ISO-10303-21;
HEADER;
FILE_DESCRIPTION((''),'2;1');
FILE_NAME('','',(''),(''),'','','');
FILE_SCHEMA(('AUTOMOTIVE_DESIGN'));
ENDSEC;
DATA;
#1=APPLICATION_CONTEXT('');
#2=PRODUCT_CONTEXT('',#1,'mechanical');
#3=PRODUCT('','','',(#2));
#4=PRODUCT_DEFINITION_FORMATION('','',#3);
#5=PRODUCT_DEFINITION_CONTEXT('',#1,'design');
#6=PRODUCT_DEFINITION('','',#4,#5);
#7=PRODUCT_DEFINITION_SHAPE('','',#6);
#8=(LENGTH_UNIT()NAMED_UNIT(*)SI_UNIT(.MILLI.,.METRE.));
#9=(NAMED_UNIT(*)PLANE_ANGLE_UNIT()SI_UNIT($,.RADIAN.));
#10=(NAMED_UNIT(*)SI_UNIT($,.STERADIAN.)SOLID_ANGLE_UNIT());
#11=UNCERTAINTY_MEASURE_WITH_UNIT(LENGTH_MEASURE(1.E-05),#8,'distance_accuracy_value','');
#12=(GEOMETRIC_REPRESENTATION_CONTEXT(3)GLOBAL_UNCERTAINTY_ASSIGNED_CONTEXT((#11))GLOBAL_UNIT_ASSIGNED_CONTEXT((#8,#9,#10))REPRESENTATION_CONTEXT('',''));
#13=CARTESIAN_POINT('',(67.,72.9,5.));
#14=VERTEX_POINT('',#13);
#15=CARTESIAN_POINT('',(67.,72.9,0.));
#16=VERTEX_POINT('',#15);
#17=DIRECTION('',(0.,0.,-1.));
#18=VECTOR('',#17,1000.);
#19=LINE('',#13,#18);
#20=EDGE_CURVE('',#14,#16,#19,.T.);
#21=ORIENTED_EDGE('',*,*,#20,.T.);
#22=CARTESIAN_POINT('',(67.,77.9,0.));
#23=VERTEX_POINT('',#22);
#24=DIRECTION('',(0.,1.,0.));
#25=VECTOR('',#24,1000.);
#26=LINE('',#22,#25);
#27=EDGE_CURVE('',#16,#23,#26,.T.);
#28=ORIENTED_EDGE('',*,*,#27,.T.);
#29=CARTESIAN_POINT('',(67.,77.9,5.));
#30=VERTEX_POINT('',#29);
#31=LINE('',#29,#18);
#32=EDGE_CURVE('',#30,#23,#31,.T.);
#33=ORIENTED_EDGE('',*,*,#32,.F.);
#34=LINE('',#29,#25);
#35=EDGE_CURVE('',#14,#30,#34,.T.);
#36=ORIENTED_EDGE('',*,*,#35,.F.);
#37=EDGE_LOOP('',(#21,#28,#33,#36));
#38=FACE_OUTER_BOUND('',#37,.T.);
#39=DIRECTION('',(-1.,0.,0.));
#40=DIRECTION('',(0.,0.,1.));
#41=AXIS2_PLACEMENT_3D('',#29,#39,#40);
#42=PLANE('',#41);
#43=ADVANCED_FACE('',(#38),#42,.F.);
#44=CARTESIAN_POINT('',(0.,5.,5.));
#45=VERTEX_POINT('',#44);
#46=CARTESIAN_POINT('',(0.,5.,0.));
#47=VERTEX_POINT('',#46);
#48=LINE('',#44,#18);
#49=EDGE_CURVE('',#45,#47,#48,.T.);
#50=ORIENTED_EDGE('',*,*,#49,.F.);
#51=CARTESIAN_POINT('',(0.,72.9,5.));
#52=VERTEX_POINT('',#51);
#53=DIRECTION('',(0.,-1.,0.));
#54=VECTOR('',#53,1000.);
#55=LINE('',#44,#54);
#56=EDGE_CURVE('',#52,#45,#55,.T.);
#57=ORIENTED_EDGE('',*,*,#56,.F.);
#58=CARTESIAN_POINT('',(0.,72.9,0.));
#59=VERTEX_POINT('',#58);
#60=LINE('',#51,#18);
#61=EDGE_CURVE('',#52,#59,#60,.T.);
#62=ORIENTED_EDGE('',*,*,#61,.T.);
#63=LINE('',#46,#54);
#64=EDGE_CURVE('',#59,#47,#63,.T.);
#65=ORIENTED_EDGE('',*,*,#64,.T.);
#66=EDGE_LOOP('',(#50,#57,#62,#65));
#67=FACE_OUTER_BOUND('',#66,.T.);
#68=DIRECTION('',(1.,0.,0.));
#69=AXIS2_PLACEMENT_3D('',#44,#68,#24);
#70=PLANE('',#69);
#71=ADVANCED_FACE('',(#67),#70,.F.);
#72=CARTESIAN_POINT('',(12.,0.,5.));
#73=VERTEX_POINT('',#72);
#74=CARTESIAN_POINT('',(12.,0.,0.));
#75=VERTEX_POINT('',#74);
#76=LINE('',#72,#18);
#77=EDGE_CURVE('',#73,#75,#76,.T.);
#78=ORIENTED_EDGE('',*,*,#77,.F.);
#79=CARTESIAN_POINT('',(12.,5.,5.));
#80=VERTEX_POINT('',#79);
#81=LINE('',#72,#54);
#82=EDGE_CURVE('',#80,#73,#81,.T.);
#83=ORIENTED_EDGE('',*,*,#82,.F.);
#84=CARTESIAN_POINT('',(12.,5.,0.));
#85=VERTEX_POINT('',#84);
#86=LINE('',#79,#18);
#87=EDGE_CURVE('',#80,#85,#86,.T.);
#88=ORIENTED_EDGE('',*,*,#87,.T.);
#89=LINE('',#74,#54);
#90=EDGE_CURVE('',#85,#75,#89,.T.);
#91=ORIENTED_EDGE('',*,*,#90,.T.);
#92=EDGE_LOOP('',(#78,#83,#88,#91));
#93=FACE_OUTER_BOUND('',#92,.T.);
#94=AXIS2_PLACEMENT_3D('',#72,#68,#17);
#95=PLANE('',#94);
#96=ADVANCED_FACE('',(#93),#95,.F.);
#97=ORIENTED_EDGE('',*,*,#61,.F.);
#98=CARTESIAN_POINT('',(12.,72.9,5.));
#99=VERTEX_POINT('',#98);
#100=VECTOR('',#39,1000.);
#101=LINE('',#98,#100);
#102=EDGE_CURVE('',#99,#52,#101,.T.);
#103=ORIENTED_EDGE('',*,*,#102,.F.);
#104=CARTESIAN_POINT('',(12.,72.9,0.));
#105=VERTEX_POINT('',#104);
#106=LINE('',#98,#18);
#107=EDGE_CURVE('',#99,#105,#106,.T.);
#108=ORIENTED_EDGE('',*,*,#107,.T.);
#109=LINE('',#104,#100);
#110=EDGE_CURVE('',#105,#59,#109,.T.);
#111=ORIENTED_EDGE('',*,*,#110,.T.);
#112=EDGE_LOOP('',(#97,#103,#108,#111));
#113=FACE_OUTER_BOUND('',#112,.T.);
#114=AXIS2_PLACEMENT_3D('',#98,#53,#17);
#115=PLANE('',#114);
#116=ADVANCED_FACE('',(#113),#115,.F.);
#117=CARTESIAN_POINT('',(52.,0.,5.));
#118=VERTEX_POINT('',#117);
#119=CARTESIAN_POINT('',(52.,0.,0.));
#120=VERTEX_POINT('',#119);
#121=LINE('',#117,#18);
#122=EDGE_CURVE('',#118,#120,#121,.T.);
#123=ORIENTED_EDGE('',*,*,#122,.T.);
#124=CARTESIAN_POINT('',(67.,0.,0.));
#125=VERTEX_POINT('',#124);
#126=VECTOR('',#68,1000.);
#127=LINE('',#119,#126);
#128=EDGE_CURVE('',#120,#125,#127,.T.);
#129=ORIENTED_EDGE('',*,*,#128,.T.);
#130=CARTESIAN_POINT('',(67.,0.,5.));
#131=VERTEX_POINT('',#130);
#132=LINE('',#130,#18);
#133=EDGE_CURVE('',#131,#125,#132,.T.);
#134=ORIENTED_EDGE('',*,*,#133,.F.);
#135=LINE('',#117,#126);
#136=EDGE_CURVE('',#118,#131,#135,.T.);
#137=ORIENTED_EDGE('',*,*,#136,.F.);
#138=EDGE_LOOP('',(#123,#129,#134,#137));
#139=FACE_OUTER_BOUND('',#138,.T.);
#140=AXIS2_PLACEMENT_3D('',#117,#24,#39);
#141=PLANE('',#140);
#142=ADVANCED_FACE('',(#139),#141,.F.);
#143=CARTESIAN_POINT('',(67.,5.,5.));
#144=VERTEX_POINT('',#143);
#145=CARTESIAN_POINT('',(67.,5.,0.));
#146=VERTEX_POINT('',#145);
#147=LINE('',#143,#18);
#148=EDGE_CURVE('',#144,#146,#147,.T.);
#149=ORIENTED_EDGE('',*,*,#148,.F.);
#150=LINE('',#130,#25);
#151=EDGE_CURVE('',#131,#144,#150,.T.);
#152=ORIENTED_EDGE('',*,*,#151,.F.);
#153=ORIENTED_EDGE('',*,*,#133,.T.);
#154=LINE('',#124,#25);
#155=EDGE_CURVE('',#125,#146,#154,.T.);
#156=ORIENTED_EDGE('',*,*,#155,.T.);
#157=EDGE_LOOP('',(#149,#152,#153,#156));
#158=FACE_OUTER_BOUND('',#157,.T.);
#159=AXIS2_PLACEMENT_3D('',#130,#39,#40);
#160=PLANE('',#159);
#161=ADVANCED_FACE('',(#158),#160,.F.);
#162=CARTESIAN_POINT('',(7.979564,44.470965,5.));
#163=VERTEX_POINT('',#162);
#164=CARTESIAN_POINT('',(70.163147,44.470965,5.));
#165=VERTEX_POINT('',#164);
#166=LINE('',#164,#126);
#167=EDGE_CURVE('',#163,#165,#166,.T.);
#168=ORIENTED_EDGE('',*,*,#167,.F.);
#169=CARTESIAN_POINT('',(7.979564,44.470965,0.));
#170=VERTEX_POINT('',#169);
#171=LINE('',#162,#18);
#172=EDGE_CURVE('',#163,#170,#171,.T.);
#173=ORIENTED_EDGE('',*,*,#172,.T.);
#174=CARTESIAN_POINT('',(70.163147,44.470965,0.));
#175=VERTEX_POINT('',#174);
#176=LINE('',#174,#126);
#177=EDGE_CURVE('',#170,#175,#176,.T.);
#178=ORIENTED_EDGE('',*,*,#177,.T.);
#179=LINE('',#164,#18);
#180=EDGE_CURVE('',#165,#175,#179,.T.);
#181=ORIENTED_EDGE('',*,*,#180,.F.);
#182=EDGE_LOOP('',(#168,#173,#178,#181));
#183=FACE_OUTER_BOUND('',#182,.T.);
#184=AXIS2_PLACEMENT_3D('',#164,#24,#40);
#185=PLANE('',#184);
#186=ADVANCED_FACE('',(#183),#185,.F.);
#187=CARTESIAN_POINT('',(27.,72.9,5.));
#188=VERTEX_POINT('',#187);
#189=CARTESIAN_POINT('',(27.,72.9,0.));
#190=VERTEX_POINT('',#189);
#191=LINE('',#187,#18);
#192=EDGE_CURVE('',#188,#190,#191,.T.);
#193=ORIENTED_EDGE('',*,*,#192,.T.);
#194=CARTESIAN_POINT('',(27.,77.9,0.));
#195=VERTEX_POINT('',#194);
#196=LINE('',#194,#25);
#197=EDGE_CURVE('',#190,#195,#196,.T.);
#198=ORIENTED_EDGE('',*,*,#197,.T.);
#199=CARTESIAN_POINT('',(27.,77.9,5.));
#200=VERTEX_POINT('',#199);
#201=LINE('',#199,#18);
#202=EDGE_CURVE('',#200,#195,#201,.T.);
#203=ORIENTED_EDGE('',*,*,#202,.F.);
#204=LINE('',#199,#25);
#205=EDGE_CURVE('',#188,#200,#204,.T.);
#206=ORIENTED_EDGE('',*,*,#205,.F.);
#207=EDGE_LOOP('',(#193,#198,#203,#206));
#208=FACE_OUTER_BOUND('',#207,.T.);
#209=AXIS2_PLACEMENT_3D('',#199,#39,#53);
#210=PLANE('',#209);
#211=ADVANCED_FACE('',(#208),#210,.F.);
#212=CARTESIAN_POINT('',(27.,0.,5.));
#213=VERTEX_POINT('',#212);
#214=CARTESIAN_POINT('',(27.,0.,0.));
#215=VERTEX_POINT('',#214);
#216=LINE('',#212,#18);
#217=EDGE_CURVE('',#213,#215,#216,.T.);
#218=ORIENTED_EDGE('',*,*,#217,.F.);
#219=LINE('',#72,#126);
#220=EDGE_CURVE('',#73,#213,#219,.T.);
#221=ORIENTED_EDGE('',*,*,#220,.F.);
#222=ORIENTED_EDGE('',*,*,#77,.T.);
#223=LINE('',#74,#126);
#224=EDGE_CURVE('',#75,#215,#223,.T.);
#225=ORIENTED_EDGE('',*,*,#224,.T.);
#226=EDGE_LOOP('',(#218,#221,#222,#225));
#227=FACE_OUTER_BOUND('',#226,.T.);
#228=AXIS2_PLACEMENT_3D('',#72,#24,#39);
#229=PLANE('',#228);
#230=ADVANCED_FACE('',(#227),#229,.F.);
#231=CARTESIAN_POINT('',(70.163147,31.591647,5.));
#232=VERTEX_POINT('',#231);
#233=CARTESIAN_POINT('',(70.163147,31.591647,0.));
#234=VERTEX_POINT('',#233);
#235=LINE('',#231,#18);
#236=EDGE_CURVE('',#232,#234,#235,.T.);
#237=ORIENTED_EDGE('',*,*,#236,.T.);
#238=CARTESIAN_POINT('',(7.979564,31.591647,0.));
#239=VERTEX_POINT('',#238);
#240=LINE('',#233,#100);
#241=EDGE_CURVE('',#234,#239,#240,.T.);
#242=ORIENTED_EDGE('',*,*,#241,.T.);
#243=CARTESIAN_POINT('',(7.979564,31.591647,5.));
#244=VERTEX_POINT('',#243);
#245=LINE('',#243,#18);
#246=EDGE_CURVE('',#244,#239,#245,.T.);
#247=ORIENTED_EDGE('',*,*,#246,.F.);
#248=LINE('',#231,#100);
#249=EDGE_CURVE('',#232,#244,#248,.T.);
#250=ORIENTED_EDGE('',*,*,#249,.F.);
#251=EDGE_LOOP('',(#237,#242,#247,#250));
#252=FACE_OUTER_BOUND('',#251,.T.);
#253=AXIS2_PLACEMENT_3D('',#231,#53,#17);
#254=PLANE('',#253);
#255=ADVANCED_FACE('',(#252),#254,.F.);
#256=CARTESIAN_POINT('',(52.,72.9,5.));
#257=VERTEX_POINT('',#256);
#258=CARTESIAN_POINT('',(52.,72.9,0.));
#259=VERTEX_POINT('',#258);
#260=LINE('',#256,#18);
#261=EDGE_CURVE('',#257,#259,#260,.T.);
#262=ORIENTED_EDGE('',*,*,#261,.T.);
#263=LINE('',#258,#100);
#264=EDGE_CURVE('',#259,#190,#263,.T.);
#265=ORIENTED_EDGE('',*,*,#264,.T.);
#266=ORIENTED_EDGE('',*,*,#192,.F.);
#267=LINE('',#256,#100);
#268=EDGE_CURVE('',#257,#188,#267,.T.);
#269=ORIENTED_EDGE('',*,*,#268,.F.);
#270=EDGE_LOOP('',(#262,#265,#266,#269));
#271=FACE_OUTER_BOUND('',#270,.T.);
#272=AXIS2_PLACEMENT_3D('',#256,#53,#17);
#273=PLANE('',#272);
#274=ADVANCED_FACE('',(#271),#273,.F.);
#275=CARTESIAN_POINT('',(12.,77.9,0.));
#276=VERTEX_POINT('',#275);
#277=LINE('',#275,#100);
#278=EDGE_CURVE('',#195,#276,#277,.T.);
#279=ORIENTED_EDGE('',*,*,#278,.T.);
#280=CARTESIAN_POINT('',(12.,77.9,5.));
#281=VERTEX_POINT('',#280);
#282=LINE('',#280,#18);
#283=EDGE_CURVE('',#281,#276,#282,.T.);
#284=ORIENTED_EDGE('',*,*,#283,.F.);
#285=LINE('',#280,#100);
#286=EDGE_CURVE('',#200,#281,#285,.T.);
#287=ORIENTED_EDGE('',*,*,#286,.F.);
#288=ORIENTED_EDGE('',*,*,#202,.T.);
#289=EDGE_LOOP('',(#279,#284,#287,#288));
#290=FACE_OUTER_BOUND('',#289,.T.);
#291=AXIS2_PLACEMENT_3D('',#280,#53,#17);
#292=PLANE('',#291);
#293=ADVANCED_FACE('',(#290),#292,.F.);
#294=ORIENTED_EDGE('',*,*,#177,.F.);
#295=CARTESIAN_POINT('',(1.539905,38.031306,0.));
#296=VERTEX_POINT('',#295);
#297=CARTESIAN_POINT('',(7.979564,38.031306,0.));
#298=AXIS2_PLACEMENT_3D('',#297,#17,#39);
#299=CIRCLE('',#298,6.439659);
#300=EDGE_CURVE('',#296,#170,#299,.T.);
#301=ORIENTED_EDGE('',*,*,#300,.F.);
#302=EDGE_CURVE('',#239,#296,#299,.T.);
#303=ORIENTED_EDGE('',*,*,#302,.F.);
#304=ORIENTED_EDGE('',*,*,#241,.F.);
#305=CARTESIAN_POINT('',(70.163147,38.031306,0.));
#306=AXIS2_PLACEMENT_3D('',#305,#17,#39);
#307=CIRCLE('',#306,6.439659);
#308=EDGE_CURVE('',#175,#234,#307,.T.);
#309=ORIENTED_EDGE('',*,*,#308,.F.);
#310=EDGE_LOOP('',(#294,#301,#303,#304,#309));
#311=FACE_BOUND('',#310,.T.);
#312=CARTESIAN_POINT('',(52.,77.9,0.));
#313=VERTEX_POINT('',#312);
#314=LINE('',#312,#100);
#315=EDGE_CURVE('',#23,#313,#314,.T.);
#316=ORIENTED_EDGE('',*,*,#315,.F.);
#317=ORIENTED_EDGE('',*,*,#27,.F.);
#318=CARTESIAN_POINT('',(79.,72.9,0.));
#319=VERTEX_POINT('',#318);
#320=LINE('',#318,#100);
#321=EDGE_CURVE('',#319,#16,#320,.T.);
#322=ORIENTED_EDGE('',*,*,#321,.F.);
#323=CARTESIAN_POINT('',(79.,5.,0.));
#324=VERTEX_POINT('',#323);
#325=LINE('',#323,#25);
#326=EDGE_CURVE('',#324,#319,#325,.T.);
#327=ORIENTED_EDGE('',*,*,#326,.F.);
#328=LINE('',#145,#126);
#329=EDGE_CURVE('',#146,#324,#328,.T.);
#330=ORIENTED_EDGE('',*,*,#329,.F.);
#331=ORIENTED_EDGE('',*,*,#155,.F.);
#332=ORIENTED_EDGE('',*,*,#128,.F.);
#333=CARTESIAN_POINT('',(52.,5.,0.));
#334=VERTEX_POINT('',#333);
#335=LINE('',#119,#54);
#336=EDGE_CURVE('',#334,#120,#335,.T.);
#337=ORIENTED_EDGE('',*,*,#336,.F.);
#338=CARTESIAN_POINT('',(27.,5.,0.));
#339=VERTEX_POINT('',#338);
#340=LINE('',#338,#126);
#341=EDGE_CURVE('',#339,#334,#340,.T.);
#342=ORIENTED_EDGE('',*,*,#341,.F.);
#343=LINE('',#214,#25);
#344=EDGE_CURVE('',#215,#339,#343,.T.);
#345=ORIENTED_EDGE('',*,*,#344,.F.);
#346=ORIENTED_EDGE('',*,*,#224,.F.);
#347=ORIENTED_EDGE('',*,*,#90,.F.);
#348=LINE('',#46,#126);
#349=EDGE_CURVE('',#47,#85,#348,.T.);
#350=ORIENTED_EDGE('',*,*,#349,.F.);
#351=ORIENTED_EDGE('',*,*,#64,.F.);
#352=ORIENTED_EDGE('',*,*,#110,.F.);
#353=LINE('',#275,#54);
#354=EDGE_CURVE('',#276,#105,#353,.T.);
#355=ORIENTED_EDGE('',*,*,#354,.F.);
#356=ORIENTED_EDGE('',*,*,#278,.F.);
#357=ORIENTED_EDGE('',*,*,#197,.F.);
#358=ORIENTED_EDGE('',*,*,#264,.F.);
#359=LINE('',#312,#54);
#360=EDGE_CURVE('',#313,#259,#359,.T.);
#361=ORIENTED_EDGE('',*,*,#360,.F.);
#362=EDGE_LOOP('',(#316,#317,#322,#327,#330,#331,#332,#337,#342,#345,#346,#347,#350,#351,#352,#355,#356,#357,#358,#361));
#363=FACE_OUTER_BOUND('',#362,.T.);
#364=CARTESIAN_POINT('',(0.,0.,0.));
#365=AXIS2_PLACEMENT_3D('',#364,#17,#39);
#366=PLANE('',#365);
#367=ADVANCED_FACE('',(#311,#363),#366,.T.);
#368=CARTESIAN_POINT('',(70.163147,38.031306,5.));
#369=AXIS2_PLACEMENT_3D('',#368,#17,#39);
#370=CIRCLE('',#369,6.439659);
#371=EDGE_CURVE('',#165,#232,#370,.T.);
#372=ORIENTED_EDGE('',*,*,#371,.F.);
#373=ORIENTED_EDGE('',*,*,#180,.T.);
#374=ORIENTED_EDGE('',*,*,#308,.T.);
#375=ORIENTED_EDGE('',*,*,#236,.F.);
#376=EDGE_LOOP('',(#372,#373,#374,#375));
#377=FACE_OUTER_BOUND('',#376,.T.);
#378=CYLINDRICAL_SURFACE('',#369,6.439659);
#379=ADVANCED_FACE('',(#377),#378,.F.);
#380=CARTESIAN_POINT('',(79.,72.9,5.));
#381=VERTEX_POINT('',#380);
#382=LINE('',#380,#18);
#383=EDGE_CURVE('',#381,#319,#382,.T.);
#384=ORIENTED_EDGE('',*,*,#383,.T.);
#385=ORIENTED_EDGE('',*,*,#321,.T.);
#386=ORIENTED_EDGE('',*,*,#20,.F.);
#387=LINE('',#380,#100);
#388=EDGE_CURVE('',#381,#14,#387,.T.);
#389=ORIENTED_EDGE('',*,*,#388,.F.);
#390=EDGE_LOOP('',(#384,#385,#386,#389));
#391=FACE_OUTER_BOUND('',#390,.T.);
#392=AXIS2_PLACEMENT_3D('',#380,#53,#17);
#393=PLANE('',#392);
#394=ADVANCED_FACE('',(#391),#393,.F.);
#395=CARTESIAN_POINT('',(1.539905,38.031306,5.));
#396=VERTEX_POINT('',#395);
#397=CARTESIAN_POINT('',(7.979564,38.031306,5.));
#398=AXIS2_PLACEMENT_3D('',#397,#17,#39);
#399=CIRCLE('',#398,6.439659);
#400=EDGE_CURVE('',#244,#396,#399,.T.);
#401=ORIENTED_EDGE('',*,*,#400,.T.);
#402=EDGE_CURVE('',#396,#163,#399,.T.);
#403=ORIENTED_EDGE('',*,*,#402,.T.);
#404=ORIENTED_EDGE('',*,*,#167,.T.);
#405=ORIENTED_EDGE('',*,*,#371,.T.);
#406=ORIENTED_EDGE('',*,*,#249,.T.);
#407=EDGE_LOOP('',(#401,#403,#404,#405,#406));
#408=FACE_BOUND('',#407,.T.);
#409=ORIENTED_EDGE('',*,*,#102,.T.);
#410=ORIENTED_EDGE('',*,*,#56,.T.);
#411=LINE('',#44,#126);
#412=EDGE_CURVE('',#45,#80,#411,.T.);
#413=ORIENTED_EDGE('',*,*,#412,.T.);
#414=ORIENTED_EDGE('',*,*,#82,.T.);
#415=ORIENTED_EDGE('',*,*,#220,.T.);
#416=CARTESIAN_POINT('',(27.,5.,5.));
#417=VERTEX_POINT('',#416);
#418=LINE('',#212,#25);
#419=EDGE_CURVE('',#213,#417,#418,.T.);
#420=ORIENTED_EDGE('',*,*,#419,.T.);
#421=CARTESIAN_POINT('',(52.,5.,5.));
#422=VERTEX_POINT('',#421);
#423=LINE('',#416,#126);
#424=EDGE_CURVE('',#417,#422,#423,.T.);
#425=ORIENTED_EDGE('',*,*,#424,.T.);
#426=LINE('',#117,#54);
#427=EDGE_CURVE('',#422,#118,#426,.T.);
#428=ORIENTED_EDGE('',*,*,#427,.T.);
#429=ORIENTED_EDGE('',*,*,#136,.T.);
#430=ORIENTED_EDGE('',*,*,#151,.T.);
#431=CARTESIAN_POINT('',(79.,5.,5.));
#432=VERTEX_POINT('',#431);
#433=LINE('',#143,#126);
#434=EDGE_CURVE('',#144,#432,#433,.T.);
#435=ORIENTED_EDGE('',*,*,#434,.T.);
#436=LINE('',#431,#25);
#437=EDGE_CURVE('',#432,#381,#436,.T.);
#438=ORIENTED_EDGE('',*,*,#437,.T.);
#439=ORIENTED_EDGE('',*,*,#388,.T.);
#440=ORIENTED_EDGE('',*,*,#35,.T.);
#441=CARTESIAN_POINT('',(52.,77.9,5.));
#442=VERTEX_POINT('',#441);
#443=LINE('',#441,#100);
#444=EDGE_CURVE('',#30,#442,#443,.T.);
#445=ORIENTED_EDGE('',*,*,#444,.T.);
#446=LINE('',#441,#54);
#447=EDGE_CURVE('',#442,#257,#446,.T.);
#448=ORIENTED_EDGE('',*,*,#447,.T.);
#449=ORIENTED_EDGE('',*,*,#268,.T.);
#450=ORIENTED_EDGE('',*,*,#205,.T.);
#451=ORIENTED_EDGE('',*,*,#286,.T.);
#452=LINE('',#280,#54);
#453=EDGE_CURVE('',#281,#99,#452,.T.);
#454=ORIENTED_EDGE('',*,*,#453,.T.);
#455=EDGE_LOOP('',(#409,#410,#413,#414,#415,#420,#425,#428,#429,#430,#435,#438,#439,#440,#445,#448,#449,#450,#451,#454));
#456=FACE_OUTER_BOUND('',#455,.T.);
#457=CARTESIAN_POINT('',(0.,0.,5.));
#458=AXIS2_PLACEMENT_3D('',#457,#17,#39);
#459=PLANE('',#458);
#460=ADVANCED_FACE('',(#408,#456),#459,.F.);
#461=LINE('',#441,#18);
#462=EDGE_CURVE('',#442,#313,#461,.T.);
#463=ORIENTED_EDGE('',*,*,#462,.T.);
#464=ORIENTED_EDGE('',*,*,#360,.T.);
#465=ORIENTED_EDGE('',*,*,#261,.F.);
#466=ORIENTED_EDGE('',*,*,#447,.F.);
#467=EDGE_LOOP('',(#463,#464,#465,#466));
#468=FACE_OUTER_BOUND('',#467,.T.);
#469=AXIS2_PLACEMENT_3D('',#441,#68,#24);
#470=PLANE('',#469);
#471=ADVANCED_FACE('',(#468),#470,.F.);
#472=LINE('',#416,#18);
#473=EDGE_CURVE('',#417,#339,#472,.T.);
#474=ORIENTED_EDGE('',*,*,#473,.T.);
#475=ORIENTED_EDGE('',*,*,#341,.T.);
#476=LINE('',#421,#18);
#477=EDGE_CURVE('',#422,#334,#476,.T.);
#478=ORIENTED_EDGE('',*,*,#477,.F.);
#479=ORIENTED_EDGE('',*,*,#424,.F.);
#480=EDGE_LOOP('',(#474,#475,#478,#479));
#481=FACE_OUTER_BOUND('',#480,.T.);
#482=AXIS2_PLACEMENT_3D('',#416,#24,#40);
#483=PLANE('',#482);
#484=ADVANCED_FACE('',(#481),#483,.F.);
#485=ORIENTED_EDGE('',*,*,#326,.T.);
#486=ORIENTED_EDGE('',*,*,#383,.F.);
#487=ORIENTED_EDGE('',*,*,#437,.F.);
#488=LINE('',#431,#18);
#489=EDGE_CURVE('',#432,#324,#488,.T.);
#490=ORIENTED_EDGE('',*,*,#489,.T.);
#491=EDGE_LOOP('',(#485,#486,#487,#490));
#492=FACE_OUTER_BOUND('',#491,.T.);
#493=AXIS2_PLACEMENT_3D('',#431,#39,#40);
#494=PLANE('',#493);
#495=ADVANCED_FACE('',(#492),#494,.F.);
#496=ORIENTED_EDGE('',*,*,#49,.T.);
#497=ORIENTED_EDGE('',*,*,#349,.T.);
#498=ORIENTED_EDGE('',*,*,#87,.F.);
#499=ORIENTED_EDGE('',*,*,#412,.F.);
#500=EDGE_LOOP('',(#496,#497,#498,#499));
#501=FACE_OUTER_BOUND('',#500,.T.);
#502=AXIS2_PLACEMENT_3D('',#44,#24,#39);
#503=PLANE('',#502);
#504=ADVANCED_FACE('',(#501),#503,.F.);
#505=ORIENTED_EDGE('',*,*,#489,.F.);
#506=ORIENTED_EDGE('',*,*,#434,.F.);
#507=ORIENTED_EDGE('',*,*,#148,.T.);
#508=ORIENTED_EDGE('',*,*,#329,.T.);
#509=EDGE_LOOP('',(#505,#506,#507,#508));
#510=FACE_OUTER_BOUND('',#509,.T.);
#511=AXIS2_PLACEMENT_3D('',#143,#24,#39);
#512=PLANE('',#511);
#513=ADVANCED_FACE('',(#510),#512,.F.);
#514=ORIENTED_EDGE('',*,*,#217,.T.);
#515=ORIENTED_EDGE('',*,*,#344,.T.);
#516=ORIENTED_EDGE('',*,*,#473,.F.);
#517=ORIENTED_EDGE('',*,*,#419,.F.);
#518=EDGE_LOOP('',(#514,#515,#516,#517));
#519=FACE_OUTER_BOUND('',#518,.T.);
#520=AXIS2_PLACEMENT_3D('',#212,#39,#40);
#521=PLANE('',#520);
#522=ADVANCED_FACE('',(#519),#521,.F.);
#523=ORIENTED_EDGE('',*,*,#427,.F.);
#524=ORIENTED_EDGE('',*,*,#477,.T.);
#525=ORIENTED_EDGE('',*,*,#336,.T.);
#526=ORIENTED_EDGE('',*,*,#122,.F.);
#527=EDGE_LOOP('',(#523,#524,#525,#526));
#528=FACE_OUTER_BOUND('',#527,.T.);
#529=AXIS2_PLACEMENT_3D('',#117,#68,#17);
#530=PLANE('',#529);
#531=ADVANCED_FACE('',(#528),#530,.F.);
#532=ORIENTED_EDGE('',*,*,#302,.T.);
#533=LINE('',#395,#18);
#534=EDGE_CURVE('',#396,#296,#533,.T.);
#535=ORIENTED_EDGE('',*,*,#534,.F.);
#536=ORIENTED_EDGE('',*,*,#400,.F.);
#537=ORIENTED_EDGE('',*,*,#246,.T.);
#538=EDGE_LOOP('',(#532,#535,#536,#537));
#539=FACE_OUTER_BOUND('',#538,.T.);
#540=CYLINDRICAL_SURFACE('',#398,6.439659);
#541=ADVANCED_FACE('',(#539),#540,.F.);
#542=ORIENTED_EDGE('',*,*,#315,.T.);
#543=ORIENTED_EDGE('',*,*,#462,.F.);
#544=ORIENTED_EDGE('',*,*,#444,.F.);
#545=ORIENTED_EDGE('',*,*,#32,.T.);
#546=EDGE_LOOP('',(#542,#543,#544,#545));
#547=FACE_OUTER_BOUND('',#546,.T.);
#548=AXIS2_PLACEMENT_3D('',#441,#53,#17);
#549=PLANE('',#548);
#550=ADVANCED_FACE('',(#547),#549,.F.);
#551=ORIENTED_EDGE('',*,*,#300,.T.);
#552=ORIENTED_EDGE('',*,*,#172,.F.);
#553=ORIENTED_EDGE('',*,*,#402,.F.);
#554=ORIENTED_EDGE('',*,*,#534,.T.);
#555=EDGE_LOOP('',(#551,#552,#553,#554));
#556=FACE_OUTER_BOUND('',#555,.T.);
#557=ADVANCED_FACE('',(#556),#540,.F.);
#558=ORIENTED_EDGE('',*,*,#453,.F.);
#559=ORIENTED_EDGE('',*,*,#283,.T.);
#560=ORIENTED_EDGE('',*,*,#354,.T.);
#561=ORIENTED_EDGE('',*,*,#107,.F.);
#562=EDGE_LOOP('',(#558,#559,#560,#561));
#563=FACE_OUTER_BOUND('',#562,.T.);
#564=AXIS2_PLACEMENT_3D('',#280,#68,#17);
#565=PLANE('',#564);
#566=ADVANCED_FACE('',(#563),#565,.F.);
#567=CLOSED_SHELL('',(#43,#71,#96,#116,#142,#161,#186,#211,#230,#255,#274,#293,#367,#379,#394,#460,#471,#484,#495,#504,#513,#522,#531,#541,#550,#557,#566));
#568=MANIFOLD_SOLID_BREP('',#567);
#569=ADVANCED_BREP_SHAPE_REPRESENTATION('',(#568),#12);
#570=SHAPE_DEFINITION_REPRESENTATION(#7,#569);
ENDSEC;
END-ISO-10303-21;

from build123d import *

# Parameters (mm, degrees)
EXTRUDE_1_DEPTH     = 5
CUT_EXTRUDE_2_DEPTH = 5


with BuildPart() as part:
    # 草图1 → 凸台-拉伸1 (new body)
    with BuildSketch(Plane.XY):
        Polygon((12, 0), (27, 0), (27, 5), (52, 5), (52, 0), (67, 0), (67, 5), (79, 5), (79, 72.9), (67, 72.9), (67, 77.9), (52, 77.9), (52, 72.9), (27, 72.9), (27, 77.9), (12, 77.9), (12, 72.9), (0, 72.9), (0, 5), (12, 5), align=None)
    extrude(amount=EXTRUDE_1_DEPTH)

    # 草图2 → 切除-拉伸2 (cut)
    with BuildSketch(Plane(origin=(0, 0, 0), x_dir=(-1, 0, 0), z_dir=(0, 0, -1))):
        with BuildLine():
            Line((-70.163147459, 44.470964867), (-7.979563682, 44.470964867))
            ThreePointArc((-7.979563682, 44.470964867), (-1.539904649, 38.031305835), (-7.979563682, 31.591646802))
            Line((-7.979563682, 31.591646802), (-70.163147459, 31.591646802))
            ThreePointArc((-70.163147459, 31.591646802), (-76.602806492, 38.031305835), (-70.163147459, 44.470964867))
        make_face()
    extrude(amount=-CUT_EXTRUDE_2_DEPTH, mode=Mode.SUBTRACT)


solid = part.part
